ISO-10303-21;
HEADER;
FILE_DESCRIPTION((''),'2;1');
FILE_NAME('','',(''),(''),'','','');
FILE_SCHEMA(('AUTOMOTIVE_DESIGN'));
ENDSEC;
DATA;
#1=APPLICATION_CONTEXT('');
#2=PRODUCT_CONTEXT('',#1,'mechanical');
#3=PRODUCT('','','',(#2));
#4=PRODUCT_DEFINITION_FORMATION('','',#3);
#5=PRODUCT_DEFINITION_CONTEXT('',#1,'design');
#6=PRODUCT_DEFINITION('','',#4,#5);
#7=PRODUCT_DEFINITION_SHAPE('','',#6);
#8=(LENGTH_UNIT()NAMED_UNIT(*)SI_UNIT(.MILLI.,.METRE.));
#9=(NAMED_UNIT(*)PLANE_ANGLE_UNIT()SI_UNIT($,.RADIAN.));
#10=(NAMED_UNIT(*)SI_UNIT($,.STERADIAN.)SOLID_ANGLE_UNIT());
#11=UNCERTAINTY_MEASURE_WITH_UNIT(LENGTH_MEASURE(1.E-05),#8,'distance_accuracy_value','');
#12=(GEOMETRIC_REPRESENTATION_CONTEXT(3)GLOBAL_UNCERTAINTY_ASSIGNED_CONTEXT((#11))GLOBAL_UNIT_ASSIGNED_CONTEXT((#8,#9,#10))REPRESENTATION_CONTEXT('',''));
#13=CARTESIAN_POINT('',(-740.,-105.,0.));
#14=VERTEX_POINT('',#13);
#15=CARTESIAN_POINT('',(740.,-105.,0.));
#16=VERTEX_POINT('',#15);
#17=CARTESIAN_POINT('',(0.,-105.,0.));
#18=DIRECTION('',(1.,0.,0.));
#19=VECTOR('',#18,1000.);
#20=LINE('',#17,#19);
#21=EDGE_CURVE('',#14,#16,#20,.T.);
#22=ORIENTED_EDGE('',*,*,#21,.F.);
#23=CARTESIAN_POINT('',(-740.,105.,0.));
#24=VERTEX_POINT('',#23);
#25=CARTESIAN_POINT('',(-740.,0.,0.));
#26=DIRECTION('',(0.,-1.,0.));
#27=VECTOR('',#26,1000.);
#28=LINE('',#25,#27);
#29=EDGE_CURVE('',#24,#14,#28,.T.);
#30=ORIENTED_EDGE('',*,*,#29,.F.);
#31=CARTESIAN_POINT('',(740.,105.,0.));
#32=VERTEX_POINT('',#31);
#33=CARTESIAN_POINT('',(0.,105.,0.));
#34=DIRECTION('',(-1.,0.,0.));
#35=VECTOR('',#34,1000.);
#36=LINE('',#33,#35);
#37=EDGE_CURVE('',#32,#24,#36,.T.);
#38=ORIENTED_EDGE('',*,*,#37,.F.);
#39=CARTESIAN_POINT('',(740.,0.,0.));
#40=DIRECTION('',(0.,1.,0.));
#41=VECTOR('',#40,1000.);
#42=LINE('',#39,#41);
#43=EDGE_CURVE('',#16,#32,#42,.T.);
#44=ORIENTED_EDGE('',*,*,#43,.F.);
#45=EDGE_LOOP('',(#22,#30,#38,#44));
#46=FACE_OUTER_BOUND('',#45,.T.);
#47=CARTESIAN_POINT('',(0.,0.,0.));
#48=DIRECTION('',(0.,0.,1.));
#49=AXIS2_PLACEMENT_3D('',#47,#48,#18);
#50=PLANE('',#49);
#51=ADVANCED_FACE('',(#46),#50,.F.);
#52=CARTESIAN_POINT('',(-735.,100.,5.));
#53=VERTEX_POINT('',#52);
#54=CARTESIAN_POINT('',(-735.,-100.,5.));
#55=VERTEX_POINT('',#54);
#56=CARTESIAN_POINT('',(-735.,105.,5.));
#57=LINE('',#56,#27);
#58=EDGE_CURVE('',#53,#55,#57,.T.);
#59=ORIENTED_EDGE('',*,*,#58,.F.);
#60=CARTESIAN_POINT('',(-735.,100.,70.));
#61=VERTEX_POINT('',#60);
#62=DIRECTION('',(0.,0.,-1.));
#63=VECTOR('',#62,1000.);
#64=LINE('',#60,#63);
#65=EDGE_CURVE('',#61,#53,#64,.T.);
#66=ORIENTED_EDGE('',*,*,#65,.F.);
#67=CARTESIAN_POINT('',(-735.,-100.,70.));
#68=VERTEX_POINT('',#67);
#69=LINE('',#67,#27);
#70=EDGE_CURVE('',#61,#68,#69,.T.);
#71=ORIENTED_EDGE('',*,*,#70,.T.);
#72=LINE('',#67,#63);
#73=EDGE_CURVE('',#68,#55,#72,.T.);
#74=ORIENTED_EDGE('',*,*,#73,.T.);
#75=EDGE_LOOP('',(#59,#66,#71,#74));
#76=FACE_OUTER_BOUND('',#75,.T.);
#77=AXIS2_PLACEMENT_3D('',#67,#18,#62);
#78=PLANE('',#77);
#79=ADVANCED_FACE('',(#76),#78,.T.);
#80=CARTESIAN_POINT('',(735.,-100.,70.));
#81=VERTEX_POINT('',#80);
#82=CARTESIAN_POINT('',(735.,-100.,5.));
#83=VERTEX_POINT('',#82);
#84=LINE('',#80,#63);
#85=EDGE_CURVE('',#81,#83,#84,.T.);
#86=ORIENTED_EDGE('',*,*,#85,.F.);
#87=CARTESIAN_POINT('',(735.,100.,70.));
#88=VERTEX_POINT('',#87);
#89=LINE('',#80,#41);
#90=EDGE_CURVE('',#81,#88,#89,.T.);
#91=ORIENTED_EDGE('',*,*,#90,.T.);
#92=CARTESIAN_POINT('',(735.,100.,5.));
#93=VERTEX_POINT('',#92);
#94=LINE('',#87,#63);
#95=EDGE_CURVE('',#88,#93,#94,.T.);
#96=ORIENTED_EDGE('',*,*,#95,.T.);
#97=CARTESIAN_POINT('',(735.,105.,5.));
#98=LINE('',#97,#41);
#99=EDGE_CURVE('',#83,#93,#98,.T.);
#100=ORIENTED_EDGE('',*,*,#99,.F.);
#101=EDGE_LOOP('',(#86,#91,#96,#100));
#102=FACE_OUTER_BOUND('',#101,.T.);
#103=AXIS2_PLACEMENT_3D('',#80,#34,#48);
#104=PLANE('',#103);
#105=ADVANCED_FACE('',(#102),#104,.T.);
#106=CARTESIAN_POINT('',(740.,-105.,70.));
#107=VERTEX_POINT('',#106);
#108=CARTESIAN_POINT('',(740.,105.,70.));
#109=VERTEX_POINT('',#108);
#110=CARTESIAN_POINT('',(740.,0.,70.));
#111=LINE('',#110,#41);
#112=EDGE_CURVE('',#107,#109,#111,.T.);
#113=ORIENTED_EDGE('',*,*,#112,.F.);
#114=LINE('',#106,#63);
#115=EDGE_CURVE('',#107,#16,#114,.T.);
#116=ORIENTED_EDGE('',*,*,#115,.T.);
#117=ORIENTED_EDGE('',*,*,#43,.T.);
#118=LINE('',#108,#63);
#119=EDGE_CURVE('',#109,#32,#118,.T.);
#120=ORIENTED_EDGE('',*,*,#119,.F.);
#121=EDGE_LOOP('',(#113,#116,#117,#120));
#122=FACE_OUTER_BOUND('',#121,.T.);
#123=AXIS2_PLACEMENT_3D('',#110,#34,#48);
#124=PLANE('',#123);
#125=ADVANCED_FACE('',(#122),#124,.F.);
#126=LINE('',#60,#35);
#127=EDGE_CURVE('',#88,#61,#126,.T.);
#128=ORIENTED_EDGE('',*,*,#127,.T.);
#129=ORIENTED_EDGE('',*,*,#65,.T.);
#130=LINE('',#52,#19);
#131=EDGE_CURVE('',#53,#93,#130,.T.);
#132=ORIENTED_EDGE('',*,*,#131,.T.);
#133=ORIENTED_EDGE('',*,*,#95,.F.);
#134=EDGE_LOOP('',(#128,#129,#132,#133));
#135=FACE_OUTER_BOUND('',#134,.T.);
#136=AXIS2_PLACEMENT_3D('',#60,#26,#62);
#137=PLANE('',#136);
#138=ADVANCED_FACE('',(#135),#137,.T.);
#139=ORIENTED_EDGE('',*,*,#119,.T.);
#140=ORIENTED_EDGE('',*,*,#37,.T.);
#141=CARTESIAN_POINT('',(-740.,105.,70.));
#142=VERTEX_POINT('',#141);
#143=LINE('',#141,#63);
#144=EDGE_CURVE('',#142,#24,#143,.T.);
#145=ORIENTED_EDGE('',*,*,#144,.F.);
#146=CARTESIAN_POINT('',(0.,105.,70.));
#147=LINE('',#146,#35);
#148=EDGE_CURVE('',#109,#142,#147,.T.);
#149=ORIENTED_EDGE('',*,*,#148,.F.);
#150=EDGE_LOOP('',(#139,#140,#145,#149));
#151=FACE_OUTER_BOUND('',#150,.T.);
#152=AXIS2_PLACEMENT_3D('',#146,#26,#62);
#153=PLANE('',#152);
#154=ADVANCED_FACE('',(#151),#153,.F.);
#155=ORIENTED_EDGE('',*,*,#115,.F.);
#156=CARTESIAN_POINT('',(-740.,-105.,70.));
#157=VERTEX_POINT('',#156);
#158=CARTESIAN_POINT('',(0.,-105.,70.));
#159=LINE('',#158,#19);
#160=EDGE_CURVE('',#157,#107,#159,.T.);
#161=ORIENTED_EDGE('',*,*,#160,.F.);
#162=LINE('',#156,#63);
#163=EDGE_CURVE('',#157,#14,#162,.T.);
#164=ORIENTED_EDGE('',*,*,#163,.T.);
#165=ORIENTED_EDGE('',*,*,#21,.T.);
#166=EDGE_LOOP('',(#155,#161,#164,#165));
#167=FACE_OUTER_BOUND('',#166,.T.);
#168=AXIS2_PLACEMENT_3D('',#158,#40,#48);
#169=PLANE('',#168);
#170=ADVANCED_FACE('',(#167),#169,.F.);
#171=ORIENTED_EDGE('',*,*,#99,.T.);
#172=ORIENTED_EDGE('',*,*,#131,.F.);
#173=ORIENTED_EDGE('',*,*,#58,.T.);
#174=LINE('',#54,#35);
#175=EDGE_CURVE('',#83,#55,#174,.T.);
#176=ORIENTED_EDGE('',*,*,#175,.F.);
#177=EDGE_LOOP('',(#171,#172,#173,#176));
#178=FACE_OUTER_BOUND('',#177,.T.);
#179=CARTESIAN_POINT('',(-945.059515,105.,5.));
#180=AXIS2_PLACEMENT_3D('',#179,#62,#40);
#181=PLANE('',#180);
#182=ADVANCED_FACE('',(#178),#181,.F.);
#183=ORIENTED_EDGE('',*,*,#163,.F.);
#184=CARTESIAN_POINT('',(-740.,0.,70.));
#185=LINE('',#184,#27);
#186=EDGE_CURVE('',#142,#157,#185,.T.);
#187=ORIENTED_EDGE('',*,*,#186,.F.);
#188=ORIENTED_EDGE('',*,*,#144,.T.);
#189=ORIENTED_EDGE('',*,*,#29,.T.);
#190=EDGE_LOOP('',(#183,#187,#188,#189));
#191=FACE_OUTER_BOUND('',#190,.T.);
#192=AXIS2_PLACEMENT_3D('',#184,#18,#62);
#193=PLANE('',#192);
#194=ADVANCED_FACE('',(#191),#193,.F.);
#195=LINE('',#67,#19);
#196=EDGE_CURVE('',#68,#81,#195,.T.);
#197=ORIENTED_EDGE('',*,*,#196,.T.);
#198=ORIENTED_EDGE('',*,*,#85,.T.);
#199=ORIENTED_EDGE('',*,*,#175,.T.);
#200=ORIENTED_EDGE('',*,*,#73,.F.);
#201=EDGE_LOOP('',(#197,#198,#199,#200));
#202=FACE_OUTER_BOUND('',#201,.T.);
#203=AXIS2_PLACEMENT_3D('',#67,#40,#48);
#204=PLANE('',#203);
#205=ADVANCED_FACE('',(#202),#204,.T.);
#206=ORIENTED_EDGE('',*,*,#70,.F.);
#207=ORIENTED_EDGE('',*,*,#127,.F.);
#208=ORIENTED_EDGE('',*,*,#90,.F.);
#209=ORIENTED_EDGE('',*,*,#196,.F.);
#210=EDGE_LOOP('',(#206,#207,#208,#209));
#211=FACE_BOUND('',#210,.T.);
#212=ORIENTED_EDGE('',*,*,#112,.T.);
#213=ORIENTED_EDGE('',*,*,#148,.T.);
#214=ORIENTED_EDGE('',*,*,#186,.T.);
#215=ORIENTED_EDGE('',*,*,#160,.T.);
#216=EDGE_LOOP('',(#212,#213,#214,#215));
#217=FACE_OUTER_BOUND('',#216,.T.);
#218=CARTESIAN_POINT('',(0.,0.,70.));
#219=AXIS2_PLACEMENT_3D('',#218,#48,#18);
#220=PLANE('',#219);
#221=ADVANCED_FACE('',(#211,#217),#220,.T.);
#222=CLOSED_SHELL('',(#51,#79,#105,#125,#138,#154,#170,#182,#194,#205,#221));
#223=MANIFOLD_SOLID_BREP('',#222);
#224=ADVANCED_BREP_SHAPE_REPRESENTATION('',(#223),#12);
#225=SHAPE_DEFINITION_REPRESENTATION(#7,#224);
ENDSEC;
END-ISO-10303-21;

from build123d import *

# Parameters (mm, degrees)
SKETCH_1_W        = 1480
SKETCH_1_H        = 210
SKETCH_1_W_2      = 1470
SKETCH_1_H_2      = 200
EXTRUDE_1_DEPTH   = 70
SKETCH_2_W        = 5
SKETCH_2_H        = 210
EXTRUDE_1_2_DEPTH = 1470


with BuildPart() as part:
    # 草图1 → Extrude 1 (new body)
    with BuildSketch(Plane.XY):
        Rectangle(SKETCH_1_W, SKETCH_1_H)
        Rectangle(SKETCH_1_W_2, SKETCH_1_H_2, mode=Mode.SUBTRACT)
    extrude(amount=EXTRUDE_1_DEPTH)

    # 草图2 → Extrude 1 2 (add)
    with BuildSketch(Plane.ZY.offset(-735)):
        with Locations((2.5, 0)):
            Rectangle(SKETCH_2_W, SKETCH_2_H)
    extrude(amount=EXTRUDE_1_2_DEPTH)


solid = part.part
